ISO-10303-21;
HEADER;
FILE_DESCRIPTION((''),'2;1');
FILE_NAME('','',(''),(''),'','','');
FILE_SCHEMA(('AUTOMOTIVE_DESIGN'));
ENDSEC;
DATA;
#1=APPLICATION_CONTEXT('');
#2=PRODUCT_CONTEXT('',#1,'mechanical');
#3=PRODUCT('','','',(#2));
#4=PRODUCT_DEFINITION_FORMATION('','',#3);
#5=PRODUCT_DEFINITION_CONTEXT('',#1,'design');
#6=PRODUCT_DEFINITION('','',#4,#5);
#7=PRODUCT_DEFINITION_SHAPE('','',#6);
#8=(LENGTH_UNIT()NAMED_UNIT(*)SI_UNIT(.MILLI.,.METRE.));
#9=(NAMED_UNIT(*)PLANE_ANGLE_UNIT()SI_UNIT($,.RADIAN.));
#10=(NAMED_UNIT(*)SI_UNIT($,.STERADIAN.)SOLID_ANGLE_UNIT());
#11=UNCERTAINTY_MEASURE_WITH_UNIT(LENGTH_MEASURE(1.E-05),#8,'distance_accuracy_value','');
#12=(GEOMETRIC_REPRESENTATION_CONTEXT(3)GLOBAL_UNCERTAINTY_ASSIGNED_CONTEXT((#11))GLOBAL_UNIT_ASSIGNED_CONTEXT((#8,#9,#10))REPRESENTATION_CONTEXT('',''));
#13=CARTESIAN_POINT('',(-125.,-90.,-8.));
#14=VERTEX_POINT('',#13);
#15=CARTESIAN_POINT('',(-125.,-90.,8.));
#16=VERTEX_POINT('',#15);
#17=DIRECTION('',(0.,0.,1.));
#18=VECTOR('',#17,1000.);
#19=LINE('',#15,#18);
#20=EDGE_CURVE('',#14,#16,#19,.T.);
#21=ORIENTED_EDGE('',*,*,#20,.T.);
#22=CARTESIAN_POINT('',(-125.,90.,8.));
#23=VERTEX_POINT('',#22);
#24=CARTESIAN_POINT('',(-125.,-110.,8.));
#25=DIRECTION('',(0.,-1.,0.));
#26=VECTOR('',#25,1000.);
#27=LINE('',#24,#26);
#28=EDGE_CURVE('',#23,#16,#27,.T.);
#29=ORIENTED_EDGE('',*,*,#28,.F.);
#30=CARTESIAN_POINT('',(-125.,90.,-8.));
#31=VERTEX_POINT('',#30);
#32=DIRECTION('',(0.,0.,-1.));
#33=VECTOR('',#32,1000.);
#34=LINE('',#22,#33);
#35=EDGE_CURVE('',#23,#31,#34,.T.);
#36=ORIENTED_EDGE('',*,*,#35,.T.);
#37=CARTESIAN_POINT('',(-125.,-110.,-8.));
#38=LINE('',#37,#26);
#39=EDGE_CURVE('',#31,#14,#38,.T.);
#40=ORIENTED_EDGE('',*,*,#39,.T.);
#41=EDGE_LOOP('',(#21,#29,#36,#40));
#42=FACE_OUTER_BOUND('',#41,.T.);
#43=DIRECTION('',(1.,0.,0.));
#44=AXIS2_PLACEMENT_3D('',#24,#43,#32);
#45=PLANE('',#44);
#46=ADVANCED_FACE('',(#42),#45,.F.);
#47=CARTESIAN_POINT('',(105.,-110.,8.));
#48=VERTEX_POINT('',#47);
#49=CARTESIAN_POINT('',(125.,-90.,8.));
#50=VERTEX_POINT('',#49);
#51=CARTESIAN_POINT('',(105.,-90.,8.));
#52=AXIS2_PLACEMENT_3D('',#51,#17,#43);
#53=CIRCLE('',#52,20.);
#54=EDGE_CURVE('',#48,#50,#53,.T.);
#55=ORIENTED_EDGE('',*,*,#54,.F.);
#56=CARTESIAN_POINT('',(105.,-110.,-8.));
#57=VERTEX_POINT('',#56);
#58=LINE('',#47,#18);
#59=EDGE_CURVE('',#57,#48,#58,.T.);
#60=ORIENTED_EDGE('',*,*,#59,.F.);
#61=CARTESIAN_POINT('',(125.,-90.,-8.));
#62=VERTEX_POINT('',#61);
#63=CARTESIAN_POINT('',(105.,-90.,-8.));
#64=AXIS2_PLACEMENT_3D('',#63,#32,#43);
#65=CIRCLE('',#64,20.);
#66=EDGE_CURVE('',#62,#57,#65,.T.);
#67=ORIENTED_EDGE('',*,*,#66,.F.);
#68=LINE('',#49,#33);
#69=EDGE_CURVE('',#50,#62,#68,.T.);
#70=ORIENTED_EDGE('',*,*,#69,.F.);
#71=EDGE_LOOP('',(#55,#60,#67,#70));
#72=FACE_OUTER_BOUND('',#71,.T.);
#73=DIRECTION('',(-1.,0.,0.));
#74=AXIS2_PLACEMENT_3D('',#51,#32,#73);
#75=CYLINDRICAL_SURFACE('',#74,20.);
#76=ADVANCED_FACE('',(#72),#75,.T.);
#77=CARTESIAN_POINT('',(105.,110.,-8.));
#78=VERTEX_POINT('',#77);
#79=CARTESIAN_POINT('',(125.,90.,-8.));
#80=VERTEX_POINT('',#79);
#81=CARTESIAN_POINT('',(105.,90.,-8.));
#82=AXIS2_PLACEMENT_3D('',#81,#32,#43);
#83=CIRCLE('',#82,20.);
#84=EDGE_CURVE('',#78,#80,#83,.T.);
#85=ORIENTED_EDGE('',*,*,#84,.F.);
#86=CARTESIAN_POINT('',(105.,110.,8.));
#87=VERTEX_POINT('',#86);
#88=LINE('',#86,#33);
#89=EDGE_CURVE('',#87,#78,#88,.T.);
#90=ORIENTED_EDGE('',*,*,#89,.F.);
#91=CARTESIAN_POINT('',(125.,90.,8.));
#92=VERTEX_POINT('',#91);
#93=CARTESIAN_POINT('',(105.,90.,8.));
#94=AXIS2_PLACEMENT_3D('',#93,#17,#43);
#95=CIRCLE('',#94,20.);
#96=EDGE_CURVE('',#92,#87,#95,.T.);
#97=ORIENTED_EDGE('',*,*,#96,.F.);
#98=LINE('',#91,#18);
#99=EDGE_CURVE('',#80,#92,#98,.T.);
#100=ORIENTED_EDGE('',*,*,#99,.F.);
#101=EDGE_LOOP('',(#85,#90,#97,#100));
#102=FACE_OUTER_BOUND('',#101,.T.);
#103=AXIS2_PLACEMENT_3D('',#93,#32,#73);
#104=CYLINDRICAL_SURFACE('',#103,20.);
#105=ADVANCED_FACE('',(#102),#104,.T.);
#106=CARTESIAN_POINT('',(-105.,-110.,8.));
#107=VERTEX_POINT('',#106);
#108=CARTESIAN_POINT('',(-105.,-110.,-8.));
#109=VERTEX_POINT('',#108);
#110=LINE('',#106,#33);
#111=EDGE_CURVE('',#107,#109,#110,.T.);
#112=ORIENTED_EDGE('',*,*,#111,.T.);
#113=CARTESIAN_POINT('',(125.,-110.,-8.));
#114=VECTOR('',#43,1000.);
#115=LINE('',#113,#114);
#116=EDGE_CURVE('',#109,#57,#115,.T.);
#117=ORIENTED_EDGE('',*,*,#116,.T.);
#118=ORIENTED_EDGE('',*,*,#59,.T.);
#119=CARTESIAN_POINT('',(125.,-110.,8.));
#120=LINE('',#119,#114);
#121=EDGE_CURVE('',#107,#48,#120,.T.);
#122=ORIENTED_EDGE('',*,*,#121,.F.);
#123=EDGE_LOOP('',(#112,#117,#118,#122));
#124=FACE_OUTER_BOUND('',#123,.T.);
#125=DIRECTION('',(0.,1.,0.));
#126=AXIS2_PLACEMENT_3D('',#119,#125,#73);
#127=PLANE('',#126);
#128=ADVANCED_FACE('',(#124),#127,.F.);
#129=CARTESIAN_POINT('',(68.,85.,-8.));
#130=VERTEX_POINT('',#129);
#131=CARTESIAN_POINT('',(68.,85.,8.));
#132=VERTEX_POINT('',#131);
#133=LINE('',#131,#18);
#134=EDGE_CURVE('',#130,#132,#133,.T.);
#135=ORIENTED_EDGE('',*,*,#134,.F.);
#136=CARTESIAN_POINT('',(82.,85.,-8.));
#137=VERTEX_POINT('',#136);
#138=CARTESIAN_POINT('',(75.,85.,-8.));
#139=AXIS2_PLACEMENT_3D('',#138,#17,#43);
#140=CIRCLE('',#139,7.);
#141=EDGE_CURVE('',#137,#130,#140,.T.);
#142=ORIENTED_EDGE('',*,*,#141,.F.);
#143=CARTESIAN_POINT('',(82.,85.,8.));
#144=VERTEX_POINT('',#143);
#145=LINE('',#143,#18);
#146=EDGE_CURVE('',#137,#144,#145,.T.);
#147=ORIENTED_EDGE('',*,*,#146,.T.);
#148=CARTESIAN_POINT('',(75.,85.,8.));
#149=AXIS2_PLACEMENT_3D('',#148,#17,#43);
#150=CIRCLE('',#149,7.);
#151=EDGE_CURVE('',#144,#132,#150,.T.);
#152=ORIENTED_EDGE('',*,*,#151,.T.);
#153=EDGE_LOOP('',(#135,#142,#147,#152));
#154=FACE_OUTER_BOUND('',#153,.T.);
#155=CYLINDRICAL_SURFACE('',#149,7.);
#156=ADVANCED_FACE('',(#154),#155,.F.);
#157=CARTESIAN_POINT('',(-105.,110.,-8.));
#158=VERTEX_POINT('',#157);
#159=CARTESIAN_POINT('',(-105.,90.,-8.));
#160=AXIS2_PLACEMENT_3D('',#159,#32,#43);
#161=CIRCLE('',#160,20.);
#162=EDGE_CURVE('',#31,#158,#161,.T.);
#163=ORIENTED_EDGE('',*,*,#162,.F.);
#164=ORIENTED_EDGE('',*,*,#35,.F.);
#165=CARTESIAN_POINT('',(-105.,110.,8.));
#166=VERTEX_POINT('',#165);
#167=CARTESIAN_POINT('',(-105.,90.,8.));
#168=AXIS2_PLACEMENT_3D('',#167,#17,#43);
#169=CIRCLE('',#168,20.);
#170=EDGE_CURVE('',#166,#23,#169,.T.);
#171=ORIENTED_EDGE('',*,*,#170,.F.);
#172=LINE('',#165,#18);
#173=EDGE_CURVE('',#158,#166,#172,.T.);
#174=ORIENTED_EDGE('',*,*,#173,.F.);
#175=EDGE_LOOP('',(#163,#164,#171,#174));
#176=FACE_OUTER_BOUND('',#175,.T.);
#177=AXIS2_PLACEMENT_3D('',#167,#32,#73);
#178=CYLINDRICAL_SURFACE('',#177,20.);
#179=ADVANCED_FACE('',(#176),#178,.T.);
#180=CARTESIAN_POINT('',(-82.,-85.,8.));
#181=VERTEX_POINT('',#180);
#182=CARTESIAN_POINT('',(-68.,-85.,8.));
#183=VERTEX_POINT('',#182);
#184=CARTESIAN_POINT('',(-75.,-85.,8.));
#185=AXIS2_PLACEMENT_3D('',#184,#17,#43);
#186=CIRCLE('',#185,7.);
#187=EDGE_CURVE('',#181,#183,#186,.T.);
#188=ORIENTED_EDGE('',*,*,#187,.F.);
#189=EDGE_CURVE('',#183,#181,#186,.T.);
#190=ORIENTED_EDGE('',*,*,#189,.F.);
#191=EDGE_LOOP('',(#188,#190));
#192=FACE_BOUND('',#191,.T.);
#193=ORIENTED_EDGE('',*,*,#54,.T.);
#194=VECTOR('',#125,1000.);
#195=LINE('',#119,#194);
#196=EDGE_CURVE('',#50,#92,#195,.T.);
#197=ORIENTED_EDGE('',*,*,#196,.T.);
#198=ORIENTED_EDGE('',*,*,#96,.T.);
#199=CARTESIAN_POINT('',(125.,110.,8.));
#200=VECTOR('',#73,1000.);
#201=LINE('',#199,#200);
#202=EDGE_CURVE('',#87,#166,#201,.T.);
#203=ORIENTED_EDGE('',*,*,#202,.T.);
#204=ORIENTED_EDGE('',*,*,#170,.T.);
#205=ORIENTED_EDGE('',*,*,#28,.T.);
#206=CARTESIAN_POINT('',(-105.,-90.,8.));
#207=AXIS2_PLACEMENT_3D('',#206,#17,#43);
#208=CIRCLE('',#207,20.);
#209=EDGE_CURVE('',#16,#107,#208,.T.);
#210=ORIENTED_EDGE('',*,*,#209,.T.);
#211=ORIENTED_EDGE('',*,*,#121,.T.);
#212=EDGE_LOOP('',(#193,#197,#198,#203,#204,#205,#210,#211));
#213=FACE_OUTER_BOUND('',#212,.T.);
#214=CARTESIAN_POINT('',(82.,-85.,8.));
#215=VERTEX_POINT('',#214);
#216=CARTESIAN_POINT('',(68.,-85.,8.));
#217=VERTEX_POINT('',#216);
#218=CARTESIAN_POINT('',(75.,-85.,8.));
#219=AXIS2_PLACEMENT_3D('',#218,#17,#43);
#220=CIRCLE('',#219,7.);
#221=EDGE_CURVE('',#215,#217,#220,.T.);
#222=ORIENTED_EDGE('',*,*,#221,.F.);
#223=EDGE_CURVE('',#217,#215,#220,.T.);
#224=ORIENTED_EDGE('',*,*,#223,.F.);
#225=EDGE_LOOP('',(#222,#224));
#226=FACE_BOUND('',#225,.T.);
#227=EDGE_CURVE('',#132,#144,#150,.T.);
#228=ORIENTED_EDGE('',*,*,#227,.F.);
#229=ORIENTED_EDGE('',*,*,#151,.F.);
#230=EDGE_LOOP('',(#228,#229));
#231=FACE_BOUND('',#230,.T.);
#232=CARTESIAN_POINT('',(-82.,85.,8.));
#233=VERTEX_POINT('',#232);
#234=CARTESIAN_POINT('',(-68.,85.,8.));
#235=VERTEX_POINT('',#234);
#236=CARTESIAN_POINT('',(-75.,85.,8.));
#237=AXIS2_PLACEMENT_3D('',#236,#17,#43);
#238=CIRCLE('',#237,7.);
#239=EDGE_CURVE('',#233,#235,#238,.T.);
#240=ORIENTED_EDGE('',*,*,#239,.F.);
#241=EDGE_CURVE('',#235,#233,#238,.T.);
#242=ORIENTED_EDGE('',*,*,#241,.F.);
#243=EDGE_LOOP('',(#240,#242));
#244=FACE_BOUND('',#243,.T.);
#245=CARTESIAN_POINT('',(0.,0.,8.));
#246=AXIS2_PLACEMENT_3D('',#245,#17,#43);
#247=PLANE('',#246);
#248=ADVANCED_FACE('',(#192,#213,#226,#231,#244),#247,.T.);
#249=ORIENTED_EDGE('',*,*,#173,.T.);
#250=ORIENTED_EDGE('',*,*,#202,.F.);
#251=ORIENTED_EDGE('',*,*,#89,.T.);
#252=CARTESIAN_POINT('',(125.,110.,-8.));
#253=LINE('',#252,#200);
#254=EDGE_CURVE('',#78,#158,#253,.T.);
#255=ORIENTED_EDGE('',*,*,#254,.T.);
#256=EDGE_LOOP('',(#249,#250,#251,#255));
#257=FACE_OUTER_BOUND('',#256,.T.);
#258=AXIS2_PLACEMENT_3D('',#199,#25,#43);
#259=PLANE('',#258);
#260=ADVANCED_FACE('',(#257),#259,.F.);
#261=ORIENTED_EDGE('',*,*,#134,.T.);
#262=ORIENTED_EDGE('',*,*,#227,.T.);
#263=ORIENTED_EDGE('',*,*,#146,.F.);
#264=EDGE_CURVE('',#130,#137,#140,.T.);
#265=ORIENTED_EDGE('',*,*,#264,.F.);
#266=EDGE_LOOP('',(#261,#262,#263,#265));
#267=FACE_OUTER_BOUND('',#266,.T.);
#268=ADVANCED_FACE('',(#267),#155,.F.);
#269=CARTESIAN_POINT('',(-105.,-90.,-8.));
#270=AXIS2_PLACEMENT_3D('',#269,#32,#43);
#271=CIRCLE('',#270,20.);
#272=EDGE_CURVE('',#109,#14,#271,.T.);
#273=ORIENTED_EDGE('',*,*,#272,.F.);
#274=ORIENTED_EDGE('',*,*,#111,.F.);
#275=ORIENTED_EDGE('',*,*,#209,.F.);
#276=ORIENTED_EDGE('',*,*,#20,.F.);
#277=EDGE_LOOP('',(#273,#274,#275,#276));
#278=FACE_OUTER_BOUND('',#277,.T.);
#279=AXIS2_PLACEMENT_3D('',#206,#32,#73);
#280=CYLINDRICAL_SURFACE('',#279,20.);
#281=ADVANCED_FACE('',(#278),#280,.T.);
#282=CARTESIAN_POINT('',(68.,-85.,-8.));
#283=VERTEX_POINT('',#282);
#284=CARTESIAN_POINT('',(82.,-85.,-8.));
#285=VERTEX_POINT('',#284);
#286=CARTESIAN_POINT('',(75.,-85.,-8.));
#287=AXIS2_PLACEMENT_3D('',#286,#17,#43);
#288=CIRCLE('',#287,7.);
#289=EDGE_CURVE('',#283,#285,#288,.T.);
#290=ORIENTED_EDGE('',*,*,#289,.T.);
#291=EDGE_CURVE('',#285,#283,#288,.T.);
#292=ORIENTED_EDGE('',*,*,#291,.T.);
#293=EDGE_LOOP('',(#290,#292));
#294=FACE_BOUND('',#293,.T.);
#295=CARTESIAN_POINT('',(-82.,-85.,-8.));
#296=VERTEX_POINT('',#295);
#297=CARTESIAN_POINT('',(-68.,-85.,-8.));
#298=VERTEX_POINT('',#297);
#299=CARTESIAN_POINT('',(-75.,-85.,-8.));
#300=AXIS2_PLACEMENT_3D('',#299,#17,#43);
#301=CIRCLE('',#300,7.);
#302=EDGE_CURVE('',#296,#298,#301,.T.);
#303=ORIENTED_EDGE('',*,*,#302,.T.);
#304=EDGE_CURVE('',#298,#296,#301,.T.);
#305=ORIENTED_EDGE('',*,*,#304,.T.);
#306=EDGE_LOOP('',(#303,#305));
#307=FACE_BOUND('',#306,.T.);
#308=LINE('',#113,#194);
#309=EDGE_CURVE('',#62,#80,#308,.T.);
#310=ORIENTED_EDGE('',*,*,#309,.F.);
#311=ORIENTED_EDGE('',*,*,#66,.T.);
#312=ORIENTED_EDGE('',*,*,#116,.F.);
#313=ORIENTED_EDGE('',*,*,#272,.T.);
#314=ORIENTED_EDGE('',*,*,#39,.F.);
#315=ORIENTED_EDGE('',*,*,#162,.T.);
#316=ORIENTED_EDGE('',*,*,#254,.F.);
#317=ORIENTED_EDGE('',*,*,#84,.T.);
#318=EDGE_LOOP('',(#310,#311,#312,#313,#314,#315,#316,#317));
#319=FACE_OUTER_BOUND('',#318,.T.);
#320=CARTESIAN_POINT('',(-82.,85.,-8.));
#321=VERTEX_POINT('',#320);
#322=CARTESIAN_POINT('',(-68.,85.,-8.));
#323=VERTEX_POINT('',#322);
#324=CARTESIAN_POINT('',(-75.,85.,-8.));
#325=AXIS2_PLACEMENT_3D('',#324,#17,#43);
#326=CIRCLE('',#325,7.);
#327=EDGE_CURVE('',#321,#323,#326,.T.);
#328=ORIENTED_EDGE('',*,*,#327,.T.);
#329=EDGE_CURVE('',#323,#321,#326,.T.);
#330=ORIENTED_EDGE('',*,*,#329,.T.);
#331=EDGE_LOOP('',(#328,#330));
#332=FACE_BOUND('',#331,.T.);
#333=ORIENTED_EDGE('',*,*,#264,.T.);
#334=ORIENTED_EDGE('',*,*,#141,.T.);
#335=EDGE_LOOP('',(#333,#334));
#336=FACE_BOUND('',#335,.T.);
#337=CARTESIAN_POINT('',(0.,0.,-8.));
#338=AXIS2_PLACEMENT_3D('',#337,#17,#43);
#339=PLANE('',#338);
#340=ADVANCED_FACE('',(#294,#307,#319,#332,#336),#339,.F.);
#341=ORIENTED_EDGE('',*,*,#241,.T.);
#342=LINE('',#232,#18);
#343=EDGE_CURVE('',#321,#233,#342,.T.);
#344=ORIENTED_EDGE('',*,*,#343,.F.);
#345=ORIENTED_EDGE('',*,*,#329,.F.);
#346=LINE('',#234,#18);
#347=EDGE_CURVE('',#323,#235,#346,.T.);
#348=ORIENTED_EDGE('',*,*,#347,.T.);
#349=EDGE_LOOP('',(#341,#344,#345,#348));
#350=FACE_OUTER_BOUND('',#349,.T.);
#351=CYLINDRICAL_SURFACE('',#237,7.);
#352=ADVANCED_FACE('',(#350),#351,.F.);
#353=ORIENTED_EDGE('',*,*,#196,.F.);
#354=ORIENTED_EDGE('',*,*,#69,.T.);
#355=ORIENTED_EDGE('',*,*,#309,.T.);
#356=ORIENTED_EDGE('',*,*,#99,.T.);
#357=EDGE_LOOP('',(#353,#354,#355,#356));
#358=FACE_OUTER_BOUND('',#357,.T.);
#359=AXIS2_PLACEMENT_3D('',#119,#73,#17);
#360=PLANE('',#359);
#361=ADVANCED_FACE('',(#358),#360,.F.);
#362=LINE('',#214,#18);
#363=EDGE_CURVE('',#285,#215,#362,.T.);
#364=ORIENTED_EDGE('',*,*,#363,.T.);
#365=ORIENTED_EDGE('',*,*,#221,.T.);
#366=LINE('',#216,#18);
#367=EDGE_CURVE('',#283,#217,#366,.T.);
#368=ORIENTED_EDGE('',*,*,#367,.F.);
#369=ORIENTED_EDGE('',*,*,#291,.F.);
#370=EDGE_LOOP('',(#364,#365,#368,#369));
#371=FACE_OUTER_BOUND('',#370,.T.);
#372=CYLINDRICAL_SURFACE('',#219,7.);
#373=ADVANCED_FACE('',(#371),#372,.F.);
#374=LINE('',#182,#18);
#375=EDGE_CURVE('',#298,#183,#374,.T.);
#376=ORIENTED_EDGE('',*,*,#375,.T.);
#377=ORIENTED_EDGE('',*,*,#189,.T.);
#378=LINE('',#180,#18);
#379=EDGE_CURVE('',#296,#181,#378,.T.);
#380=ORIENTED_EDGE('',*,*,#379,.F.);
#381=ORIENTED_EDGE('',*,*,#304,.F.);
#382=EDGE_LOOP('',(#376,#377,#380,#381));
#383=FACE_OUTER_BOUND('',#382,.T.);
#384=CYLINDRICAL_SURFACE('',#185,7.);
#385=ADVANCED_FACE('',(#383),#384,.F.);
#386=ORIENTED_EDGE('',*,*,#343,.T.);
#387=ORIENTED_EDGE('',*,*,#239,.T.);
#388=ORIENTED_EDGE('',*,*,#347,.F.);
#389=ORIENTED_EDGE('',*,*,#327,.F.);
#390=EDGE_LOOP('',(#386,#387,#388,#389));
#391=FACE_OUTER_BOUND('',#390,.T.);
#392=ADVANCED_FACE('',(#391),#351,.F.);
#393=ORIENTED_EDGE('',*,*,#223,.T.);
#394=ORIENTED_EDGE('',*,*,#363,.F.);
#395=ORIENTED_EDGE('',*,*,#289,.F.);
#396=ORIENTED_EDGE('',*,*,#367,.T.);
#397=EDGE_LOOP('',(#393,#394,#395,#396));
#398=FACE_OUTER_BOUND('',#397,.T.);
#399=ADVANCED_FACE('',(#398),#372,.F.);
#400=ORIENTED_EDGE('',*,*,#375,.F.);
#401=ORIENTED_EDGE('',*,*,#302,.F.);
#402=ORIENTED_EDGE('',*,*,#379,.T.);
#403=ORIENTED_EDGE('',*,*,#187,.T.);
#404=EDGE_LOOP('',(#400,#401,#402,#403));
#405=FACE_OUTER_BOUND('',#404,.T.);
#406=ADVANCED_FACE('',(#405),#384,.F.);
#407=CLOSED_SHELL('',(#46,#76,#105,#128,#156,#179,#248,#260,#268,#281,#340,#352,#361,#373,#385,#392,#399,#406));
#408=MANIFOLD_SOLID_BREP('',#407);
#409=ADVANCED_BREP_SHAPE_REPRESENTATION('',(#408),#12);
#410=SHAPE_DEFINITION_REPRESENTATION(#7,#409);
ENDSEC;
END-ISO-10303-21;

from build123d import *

# Parameters (mm, degrees)
SKETCH1_W           = 250
SKETCH1_H           = 220
BOSS_EXTRUDE1_DEPTH = 8
F_14_HOLE1_D        = 14
FILLET2_R           = 20


with BuildPart() as part:
    # Sketch1 → Boss-Extrude1 (new, symmetric)
    with BuildSketch(Plane.XY):
        Rectangle(SKETCH1_W, SKETCH1_H)
    extrude(amount=BOSS_EXTRUDE1_DEPTH, both=True)

    # Ø14 Hole1 (through all)
    with Locations(Plane.XY.offset(8)):
        with Locations((-75, 85), (75, 85), (75, -85), (-75, -85)):
            Hole(F_14_HOLE1_D / 2)

    # Fillet2
    fillet2_edges = [part.edges().sort_by_distance(p)[0] for p in [
        (-125, 110, 0),
        (125, 110, 0),
        (125, -110, 0),
        (-125, -110, 0),
    ]]
    fillet(fillet2_edges, radius=FILLET2_R)


solid = part.part
